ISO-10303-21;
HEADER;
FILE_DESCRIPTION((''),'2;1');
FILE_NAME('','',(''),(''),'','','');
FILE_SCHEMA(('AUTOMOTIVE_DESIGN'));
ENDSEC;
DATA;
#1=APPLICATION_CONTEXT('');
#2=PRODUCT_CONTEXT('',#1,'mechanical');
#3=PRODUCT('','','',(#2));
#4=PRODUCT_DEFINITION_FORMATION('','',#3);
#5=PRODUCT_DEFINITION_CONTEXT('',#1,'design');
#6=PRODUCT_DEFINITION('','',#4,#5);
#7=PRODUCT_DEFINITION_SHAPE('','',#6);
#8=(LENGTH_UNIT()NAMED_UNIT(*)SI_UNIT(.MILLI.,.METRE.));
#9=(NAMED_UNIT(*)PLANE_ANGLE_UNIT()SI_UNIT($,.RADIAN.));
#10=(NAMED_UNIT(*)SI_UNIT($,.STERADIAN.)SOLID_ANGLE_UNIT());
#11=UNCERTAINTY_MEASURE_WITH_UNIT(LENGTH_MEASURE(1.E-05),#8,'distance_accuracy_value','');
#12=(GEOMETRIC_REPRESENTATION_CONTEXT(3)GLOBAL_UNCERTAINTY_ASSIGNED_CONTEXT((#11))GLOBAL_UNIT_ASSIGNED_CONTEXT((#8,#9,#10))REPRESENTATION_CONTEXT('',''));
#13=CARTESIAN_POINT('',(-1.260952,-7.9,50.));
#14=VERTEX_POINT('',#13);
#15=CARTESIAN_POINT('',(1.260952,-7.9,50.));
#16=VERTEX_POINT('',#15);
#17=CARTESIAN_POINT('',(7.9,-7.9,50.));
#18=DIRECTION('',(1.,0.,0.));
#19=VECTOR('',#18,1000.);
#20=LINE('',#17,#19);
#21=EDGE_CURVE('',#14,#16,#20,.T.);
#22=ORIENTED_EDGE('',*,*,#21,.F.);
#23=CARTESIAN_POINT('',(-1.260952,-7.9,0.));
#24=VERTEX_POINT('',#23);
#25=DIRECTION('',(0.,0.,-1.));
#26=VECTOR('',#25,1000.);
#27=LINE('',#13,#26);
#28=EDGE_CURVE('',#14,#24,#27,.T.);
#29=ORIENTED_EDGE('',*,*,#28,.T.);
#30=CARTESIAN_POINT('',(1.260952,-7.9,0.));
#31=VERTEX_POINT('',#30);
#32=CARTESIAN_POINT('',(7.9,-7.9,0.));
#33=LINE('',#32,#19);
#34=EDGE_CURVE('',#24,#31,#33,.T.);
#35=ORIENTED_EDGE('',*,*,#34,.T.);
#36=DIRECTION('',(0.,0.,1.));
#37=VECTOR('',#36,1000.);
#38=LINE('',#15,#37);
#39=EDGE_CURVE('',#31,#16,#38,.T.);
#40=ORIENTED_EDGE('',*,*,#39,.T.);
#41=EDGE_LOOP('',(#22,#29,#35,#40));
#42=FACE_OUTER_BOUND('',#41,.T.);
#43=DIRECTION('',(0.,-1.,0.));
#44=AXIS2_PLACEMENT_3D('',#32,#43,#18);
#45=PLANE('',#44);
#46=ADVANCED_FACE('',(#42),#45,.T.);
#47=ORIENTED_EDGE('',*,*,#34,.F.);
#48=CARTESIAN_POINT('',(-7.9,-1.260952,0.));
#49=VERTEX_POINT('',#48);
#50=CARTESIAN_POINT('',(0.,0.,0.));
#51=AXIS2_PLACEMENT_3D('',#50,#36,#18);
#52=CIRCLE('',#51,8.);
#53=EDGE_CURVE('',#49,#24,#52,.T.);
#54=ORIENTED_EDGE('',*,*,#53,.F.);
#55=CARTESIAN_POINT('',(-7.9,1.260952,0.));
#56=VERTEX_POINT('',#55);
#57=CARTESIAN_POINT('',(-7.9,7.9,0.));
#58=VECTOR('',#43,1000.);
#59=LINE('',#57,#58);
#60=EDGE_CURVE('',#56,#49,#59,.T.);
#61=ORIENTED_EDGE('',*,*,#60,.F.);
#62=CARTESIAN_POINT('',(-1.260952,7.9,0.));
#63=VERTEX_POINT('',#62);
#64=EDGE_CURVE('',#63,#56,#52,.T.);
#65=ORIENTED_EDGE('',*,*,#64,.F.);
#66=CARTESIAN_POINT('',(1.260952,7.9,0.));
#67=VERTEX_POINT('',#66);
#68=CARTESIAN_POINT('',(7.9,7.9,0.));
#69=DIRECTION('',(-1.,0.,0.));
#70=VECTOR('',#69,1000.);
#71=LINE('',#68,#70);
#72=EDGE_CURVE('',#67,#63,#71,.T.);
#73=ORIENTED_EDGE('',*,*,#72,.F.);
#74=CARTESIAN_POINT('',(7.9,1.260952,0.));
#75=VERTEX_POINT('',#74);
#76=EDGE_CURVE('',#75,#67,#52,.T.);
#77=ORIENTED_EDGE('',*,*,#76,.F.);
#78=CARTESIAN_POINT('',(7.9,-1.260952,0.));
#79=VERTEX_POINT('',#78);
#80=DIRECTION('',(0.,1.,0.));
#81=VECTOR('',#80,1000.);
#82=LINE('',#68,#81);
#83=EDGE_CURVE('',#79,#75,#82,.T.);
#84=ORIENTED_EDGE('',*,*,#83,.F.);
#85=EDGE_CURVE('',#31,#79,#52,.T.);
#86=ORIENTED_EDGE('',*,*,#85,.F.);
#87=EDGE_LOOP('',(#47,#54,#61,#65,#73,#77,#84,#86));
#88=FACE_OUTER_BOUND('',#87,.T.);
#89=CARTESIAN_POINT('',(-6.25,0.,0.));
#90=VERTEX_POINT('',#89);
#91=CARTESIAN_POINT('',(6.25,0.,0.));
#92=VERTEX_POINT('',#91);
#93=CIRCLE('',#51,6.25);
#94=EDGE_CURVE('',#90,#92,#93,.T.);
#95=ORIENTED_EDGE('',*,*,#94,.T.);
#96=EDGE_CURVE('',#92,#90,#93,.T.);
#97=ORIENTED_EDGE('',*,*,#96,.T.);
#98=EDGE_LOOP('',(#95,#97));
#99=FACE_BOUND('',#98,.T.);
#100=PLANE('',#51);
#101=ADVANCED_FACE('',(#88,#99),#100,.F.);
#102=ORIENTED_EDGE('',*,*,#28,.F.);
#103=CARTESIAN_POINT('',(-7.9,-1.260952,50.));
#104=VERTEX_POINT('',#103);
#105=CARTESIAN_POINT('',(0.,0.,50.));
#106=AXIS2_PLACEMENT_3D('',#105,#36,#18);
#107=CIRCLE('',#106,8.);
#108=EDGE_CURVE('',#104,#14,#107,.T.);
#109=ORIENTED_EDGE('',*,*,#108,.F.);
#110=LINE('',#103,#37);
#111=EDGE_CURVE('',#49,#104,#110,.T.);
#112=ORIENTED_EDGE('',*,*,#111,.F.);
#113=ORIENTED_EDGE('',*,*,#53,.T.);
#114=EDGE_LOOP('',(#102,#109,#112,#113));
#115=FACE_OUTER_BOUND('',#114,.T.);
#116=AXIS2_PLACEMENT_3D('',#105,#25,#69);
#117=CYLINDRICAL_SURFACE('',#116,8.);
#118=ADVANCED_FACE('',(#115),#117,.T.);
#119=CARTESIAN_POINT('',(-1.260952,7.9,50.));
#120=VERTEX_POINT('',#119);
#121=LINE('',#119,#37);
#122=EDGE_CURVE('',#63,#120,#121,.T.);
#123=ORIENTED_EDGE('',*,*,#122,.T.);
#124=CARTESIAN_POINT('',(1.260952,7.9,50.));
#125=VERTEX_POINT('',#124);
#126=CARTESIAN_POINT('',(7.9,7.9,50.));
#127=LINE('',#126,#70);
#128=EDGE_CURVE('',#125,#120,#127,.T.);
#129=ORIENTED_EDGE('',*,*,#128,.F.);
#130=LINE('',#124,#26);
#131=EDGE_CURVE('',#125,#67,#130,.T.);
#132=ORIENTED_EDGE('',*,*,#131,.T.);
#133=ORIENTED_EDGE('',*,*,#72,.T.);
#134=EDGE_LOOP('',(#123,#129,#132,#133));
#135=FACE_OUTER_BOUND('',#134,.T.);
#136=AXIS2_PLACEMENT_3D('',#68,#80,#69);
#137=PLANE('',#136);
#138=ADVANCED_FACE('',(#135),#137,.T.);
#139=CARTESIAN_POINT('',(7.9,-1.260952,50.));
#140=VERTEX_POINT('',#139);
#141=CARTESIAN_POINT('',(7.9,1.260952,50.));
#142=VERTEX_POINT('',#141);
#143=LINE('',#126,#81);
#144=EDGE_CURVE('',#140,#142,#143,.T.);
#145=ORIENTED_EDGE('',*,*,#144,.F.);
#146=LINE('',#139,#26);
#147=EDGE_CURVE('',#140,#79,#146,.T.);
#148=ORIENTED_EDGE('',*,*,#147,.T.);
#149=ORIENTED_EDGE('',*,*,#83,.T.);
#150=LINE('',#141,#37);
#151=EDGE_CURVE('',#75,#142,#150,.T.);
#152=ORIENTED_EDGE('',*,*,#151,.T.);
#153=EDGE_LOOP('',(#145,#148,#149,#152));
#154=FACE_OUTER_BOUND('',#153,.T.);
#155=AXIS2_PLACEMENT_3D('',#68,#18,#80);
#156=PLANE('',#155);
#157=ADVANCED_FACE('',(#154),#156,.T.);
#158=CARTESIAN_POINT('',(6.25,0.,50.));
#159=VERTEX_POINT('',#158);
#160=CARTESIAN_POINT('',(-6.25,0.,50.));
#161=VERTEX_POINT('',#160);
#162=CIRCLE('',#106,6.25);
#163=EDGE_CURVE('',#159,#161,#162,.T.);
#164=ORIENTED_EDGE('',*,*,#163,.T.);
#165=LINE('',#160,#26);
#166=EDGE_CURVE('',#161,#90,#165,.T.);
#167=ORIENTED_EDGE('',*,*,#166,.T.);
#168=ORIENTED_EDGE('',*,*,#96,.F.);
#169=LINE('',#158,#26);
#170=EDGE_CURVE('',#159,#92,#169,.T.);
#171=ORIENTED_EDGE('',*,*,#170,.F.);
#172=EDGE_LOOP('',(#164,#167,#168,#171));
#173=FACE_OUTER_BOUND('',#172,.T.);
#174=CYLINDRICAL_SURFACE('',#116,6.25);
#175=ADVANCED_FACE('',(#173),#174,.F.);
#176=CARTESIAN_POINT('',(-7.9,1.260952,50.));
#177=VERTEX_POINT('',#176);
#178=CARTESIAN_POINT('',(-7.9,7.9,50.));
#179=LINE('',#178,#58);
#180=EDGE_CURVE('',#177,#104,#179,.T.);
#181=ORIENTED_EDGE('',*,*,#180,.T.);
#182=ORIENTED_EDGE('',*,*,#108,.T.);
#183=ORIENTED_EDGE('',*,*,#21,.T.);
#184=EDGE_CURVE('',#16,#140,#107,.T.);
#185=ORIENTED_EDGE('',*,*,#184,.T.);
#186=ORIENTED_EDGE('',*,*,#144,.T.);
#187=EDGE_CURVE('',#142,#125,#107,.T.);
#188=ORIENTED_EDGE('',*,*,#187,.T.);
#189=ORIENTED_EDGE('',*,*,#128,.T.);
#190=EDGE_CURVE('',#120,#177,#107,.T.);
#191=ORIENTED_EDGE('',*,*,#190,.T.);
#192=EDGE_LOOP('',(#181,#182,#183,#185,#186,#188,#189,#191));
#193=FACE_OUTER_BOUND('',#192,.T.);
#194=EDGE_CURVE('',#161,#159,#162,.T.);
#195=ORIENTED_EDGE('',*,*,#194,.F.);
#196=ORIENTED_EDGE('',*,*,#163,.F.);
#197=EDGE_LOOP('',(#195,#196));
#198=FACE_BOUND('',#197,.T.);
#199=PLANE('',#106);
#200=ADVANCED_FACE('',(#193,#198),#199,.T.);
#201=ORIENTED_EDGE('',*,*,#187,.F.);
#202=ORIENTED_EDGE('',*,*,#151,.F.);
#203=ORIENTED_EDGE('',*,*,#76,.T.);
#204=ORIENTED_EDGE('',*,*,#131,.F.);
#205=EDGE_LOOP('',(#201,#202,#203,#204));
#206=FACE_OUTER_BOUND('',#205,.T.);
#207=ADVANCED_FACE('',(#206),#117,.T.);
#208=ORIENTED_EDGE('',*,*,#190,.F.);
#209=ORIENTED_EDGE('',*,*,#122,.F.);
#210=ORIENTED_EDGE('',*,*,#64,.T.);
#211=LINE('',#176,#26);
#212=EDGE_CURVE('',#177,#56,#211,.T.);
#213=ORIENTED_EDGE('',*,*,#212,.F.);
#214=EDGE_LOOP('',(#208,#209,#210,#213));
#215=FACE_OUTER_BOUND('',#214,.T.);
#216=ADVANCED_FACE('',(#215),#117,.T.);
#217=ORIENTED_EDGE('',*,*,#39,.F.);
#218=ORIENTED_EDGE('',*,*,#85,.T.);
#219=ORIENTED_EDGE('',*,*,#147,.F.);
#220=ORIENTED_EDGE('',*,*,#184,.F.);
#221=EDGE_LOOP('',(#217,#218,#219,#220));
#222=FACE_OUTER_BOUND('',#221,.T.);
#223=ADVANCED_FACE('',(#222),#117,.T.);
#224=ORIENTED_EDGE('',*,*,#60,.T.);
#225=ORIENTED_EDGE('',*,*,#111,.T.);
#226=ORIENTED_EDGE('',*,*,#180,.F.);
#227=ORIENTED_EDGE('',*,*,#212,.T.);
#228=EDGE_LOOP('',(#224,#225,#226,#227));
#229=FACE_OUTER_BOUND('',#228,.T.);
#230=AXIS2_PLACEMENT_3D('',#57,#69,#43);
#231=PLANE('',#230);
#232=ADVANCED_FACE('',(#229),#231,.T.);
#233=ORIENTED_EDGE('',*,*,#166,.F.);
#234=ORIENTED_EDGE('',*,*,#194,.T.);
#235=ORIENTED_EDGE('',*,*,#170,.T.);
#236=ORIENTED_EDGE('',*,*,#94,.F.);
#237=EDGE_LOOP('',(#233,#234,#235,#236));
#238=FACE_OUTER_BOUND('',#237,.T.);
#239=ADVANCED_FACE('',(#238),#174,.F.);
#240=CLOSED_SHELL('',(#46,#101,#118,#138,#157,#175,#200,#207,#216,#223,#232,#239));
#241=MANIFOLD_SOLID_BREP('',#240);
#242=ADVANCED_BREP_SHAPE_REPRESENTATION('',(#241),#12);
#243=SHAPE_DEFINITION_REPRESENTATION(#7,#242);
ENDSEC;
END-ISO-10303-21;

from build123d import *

# Parameters (mm, degrees)
SKETCH1_R           = 8
SKETCH1_R_2         = 6.25
BOSS_EXTRUDE1_DEPTH = 50
SKETCH2_W           = 20.877121254
SKETCH2_H           = 20.159055414
SKETCH2_W_2         = 15.8
SKETCH2_H_2         = 15.8
CUT_EXTRUDE1_DEPTH  = 50


with BuildPart() as part:
    # Sketch1 → Boss-Extrude1 (new body)
    with BuildSketch(Plane.XY):
        Circle(SKETCH1_R)
        Circle(SKETCH1_R_2, mode=Mode.SUBTRACT)
    extrude(amount=BOSS_EXTRUDE1_DEPTH)

    # Sketch2 → Cut-Extrude1 (cut)
    with BuildSketch(Plane.XY.offset(50)):
        Rectangle(SKETCH2_W, SKETCH2_H)
        Rectangle(SKETCH2_W_2, SKETCH2_H_2, mode=Mode.SUBTRACT)
    extrude(amount=-CUT_EXTRUDE1_DEPTH, mode=Mode.SUBTRACT)


solid = part.part
